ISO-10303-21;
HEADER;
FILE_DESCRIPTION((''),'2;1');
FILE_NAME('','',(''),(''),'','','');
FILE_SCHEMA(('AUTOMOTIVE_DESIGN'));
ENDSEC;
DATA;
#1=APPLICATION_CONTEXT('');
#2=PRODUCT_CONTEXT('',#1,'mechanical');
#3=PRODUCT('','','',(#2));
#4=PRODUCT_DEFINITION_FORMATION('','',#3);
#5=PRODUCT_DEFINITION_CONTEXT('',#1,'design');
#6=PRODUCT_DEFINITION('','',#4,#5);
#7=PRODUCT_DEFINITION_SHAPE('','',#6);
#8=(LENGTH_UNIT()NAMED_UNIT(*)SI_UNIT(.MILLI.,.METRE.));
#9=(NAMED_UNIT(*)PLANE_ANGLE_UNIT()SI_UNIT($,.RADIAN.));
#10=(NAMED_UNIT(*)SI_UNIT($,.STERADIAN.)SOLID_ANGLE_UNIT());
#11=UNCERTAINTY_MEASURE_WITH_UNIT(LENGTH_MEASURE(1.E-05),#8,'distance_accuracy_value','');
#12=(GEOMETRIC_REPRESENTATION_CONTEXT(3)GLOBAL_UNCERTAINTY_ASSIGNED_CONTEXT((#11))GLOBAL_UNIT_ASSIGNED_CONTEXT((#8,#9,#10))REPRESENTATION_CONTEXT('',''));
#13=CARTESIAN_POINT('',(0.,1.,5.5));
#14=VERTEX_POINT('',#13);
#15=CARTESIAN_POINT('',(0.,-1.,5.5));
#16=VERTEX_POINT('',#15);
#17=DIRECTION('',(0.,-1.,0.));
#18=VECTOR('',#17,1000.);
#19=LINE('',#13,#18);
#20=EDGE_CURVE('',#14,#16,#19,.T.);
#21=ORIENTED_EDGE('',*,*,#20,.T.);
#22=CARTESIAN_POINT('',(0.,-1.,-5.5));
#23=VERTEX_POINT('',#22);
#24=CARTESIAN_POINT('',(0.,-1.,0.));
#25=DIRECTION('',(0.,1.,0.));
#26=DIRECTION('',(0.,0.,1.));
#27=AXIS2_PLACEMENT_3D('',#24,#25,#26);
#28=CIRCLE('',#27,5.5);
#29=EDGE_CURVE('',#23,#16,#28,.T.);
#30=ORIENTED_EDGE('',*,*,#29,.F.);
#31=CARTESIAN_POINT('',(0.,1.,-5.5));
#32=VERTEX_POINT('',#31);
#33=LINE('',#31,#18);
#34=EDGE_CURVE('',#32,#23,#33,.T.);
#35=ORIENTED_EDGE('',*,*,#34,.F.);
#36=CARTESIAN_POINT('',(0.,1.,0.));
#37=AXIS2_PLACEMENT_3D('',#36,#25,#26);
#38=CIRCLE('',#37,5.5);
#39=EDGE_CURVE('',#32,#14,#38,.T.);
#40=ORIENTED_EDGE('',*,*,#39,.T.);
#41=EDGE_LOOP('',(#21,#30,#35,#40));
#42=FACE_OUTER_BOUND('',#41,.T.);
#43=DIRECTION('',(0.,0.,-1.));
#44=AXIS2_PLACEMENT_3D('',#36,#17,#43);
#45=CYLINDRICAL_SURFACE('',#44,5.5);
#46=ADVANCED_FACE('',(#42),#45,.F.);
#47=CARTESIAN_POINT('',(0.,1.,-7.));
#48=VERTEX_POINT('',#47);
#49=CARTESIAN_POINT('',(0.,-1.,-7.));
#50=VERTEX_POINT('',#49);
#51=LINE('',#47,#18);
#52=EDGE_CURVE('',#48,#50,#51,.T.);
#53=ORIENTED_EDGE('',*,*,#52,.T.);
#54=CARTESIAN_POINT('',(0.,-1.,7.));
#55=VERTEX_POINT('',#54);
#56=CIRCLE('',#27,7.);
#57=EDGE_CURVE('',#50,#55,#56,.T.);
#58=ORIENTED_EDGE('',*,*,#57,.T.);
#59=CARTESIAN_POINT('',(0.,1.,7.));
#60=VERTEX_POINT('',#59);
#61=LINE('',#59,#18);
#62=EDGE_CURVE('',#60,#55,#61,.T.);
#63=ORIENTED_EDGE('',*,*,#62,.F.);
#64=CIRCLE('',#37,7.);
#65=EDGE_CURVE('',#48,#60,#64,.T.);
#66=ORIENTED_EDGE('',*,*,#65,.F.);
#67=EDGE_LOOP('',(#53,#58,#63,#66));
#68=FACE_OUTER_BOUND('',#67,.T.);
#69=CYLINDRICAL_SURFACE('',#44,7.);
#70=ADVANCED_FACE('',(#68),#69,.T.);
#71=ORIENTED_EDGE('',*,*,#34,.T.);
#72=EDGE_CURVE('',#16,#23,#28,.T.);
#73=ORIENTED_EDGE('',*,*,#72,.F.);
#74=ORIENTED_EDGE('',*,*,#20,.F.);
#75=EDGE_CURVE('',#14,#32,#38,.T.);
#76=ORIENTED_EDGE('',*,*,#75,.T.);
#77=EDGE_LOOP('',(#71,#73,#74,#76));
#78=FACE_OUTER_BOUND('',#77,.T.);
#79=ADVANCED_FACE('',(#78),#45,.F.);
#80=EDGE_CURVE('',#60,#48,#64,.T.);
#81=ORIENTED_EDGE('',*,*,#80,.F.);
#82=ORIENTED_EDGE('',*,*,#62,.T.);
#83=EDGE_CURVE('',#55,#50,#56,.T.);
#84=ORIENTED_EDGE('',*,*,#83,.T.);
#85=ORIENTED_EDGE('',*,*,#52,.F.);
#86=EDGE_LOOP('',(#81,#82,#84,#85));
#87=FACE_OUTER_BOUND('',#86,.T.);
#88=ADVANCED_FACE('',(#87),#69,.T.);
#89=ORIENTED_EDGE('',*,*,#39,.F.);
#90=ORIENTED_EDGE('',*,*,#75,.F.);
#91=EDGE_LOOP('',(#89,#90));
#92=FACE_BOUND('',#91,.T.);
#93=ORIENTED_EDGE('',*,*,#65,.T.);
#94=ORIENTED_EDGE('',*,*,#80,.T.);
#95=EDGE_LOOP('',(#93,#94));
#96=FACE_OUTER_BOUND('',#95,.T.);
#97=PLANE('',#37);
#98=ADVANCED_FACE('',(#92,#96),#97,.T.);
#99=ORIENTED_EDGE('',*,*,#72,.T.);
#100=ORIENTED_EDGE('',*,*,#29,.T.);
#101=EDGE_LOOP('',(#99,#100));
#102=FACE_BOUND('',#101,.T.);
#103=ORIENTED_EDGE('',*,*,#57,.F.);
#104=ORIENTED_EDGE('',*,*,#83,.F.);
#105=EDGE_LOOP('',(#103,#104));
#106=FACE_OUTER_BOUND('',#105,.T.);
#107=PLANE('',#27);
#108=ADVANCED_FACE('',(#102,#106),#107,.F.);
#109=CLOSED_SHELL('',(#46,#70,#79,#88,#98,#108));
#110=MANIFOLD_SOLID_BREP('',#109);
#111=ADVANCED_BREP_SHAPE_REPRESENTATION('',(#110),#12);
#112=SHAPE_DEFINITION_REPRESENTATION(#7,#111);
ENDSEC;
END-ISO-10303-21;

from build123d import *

# Parameters (mm, degrees)
SKETCH1_R           = 7
SKETCH1_R_2         = 5.5
BOSS_EXTRUDE1_DEPTH = 1


with BuildPart() as part:
    # Sketch1 → Boss-Extrude1 (new, symmetric)
    with BuildSketch(Plane(origin=(0, 0, 0), x_dir=(1, 0, 0), z_dir=(0, 1, 0))):
        with Locations(Location((0, 0, 0), (0, 0, 270))):
            Circle(SKETCH1_R)
        with Locations(Location((0, 0, 0), (0, 0, 270))):
            Circle(SKETCH1_R_2, mode=Mode.SUBTRACT)
    extrude(amount=BOSS_EXTRUDE1_DEPTH, both=True)


solid = part.part
